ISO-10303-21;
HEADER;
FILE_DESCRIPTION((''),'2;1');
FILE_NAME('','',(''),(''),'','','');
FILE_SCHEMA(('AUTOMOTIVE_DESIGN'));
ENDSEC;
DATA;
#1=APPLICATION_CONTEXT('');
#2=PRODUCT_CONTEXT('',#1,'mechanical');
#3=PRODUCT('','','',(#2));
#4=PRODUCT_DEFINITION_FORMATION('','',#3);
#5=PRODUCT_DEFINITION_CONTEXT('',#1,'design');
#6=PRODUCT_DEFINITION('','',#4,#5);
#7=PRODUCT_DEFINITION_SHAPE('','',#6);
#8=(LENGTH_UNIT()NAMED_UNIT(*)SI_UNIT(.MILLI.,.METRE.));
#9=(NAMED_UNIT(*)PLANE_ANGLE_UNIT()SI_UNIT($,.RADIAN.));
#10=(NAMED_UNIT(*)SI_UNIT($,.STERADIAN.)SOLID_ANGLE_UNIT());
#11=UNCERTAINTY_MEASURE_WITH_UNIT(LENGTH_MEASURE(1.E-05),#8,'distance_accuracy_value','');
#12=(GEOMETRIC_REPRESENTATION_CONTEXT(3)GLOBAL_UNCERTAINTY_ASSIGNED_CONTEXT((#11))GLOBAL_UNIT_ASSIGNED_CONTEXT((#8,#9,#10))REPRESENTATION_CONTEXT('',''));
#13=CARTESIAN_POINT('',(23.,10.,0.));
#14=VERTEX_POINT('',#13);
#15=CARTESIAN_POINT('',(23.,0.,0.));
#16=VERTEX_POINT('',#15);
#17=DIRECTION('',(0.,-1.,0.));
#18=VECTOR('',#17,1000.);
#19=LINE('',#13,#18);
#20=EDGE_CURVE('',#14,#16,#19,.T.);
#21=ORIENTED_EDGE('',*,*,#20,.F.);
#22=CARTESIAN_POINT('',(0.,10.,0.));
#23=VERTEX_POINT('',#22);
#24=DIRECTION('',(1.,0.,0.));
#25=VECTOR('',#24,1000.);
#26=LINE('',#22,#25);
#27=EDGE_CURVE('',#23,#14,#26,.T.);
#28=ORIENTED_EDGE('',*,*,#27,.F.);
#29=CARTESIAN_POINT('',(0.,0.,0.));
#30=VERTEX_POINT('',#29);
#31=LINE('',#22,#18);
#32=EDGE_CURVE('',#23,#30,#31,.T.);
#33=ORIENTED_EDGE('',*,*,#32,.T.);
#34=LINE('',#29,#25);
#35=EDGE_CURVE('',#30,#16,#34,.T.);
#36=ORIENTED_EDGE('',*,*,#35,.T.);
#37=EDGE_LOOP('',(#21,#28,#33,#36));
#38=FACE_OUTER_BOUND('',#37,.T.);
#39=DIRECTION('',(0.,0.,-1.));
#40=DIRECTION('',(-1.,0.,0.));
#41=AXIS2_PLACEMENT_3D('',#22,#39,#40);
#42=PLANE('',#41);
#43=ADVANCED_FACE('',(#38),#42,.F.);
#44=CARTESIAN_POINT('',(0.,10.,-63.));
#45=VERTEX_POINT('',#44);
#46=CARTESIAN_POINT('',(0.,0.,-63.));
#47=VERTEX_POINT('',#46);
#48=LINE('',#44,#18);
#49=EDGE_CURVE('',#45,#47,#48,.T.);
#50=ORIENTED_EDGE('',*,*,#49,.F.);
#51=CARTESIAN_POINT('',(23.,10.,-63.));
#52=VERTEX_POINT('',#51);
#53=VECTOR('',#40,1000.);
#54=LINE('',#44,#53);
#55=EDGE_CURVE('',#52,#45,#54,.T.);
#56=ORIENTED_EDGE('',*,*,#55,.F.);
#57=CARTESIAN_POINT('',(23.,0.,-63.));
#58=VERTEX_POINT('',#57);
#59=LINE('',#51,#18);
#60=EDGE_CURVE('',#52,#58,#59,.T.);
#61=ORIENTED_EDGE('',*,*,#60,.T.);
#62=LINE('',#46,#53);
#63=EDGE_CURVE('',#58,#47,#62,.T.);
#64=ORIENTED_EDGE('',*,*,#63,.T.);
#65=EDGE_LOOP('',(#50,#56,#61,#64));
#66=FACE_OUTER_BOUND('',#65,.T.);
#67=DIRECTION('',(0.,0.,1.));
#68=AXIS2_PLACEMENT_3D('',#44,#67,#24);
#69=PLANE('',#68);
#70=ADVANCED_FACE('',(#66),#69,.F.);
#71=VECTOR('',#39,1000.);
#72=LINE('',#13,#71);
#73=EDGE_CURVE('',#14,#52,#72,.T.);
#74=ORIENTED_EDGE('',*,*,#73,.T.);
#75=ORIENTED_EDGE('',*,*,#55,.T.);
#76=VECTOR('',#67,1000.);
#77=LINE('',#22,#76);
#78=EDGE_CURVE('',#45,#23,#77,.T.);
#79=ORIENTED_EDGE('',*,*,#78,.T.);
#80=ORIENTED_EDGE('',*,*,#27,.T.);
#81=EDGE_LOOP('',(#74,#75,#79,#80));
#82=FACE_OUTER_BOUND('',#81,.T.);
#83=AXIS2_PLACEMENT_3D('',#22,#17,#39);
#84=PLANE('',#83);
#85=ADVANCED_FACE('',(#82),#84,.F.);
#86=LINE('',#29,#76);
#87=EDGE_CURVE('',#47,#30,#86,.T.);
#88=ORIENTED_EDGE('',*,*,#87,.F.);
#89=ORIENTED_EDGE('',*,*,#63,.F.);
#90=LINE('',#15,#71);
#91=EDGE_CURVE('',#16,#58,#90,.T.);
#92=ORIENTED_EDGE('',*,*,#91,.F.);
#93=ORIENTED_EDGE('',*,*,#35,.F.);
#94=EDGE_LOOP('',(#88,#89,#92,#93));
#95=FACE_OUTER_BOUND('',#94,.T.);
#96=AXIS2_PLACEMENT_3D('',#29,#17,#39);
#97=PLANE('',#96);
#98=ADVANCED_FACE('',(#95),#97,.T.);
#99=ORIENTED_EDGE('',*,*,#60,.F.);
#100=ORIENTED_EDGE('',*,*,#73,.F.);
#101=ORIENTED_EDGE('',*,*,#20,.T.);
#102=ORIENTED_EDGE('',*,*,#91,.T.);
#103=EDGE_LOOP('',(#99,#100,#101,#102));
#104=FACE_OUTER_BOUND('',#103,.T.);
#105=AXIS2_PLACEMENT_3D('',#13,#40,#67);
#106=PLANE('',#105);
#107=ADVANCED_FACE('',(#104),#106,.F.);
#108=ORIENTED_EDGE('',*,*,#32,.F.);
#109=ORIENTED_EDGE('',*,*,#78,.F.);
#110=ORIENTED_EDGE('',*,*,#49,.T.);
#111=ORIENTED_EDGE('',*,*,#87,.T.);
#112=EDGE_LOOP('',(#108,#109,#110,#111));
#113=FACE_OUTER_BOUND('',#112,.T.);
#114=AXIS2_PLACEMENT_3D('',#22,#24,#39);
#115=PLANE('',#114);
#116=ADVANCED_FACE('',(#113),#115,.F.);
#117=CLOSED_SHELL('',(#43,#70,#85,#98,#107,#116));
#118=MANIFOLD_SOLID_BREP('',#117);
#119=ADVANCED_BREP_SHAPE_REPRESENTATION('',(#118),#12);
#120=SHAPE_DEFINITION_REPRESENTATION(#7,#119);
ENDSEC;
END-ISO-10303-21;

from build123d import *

# Parameters (mm, degrees)
SKETCH_1_W      = 23
SKETCH_1_H      = 63
EXTRUDE_1_DEPTH = 10


with BuildPart() as part:
    # 草图1 → 凸台-拉伸1 (new body)
    with BuildSketch(Plane(origin=(0, 0, 0), x_dir=(1, 0, 0), z_dir=(0, 1, 0))):
        with Locations((11.5, 31.5)):
            Rectangle(SKETCH_1_W, SKETCH_1_H)
    extrude(amount=EXTRUDE_1_DEPTH)


solid = part.part
